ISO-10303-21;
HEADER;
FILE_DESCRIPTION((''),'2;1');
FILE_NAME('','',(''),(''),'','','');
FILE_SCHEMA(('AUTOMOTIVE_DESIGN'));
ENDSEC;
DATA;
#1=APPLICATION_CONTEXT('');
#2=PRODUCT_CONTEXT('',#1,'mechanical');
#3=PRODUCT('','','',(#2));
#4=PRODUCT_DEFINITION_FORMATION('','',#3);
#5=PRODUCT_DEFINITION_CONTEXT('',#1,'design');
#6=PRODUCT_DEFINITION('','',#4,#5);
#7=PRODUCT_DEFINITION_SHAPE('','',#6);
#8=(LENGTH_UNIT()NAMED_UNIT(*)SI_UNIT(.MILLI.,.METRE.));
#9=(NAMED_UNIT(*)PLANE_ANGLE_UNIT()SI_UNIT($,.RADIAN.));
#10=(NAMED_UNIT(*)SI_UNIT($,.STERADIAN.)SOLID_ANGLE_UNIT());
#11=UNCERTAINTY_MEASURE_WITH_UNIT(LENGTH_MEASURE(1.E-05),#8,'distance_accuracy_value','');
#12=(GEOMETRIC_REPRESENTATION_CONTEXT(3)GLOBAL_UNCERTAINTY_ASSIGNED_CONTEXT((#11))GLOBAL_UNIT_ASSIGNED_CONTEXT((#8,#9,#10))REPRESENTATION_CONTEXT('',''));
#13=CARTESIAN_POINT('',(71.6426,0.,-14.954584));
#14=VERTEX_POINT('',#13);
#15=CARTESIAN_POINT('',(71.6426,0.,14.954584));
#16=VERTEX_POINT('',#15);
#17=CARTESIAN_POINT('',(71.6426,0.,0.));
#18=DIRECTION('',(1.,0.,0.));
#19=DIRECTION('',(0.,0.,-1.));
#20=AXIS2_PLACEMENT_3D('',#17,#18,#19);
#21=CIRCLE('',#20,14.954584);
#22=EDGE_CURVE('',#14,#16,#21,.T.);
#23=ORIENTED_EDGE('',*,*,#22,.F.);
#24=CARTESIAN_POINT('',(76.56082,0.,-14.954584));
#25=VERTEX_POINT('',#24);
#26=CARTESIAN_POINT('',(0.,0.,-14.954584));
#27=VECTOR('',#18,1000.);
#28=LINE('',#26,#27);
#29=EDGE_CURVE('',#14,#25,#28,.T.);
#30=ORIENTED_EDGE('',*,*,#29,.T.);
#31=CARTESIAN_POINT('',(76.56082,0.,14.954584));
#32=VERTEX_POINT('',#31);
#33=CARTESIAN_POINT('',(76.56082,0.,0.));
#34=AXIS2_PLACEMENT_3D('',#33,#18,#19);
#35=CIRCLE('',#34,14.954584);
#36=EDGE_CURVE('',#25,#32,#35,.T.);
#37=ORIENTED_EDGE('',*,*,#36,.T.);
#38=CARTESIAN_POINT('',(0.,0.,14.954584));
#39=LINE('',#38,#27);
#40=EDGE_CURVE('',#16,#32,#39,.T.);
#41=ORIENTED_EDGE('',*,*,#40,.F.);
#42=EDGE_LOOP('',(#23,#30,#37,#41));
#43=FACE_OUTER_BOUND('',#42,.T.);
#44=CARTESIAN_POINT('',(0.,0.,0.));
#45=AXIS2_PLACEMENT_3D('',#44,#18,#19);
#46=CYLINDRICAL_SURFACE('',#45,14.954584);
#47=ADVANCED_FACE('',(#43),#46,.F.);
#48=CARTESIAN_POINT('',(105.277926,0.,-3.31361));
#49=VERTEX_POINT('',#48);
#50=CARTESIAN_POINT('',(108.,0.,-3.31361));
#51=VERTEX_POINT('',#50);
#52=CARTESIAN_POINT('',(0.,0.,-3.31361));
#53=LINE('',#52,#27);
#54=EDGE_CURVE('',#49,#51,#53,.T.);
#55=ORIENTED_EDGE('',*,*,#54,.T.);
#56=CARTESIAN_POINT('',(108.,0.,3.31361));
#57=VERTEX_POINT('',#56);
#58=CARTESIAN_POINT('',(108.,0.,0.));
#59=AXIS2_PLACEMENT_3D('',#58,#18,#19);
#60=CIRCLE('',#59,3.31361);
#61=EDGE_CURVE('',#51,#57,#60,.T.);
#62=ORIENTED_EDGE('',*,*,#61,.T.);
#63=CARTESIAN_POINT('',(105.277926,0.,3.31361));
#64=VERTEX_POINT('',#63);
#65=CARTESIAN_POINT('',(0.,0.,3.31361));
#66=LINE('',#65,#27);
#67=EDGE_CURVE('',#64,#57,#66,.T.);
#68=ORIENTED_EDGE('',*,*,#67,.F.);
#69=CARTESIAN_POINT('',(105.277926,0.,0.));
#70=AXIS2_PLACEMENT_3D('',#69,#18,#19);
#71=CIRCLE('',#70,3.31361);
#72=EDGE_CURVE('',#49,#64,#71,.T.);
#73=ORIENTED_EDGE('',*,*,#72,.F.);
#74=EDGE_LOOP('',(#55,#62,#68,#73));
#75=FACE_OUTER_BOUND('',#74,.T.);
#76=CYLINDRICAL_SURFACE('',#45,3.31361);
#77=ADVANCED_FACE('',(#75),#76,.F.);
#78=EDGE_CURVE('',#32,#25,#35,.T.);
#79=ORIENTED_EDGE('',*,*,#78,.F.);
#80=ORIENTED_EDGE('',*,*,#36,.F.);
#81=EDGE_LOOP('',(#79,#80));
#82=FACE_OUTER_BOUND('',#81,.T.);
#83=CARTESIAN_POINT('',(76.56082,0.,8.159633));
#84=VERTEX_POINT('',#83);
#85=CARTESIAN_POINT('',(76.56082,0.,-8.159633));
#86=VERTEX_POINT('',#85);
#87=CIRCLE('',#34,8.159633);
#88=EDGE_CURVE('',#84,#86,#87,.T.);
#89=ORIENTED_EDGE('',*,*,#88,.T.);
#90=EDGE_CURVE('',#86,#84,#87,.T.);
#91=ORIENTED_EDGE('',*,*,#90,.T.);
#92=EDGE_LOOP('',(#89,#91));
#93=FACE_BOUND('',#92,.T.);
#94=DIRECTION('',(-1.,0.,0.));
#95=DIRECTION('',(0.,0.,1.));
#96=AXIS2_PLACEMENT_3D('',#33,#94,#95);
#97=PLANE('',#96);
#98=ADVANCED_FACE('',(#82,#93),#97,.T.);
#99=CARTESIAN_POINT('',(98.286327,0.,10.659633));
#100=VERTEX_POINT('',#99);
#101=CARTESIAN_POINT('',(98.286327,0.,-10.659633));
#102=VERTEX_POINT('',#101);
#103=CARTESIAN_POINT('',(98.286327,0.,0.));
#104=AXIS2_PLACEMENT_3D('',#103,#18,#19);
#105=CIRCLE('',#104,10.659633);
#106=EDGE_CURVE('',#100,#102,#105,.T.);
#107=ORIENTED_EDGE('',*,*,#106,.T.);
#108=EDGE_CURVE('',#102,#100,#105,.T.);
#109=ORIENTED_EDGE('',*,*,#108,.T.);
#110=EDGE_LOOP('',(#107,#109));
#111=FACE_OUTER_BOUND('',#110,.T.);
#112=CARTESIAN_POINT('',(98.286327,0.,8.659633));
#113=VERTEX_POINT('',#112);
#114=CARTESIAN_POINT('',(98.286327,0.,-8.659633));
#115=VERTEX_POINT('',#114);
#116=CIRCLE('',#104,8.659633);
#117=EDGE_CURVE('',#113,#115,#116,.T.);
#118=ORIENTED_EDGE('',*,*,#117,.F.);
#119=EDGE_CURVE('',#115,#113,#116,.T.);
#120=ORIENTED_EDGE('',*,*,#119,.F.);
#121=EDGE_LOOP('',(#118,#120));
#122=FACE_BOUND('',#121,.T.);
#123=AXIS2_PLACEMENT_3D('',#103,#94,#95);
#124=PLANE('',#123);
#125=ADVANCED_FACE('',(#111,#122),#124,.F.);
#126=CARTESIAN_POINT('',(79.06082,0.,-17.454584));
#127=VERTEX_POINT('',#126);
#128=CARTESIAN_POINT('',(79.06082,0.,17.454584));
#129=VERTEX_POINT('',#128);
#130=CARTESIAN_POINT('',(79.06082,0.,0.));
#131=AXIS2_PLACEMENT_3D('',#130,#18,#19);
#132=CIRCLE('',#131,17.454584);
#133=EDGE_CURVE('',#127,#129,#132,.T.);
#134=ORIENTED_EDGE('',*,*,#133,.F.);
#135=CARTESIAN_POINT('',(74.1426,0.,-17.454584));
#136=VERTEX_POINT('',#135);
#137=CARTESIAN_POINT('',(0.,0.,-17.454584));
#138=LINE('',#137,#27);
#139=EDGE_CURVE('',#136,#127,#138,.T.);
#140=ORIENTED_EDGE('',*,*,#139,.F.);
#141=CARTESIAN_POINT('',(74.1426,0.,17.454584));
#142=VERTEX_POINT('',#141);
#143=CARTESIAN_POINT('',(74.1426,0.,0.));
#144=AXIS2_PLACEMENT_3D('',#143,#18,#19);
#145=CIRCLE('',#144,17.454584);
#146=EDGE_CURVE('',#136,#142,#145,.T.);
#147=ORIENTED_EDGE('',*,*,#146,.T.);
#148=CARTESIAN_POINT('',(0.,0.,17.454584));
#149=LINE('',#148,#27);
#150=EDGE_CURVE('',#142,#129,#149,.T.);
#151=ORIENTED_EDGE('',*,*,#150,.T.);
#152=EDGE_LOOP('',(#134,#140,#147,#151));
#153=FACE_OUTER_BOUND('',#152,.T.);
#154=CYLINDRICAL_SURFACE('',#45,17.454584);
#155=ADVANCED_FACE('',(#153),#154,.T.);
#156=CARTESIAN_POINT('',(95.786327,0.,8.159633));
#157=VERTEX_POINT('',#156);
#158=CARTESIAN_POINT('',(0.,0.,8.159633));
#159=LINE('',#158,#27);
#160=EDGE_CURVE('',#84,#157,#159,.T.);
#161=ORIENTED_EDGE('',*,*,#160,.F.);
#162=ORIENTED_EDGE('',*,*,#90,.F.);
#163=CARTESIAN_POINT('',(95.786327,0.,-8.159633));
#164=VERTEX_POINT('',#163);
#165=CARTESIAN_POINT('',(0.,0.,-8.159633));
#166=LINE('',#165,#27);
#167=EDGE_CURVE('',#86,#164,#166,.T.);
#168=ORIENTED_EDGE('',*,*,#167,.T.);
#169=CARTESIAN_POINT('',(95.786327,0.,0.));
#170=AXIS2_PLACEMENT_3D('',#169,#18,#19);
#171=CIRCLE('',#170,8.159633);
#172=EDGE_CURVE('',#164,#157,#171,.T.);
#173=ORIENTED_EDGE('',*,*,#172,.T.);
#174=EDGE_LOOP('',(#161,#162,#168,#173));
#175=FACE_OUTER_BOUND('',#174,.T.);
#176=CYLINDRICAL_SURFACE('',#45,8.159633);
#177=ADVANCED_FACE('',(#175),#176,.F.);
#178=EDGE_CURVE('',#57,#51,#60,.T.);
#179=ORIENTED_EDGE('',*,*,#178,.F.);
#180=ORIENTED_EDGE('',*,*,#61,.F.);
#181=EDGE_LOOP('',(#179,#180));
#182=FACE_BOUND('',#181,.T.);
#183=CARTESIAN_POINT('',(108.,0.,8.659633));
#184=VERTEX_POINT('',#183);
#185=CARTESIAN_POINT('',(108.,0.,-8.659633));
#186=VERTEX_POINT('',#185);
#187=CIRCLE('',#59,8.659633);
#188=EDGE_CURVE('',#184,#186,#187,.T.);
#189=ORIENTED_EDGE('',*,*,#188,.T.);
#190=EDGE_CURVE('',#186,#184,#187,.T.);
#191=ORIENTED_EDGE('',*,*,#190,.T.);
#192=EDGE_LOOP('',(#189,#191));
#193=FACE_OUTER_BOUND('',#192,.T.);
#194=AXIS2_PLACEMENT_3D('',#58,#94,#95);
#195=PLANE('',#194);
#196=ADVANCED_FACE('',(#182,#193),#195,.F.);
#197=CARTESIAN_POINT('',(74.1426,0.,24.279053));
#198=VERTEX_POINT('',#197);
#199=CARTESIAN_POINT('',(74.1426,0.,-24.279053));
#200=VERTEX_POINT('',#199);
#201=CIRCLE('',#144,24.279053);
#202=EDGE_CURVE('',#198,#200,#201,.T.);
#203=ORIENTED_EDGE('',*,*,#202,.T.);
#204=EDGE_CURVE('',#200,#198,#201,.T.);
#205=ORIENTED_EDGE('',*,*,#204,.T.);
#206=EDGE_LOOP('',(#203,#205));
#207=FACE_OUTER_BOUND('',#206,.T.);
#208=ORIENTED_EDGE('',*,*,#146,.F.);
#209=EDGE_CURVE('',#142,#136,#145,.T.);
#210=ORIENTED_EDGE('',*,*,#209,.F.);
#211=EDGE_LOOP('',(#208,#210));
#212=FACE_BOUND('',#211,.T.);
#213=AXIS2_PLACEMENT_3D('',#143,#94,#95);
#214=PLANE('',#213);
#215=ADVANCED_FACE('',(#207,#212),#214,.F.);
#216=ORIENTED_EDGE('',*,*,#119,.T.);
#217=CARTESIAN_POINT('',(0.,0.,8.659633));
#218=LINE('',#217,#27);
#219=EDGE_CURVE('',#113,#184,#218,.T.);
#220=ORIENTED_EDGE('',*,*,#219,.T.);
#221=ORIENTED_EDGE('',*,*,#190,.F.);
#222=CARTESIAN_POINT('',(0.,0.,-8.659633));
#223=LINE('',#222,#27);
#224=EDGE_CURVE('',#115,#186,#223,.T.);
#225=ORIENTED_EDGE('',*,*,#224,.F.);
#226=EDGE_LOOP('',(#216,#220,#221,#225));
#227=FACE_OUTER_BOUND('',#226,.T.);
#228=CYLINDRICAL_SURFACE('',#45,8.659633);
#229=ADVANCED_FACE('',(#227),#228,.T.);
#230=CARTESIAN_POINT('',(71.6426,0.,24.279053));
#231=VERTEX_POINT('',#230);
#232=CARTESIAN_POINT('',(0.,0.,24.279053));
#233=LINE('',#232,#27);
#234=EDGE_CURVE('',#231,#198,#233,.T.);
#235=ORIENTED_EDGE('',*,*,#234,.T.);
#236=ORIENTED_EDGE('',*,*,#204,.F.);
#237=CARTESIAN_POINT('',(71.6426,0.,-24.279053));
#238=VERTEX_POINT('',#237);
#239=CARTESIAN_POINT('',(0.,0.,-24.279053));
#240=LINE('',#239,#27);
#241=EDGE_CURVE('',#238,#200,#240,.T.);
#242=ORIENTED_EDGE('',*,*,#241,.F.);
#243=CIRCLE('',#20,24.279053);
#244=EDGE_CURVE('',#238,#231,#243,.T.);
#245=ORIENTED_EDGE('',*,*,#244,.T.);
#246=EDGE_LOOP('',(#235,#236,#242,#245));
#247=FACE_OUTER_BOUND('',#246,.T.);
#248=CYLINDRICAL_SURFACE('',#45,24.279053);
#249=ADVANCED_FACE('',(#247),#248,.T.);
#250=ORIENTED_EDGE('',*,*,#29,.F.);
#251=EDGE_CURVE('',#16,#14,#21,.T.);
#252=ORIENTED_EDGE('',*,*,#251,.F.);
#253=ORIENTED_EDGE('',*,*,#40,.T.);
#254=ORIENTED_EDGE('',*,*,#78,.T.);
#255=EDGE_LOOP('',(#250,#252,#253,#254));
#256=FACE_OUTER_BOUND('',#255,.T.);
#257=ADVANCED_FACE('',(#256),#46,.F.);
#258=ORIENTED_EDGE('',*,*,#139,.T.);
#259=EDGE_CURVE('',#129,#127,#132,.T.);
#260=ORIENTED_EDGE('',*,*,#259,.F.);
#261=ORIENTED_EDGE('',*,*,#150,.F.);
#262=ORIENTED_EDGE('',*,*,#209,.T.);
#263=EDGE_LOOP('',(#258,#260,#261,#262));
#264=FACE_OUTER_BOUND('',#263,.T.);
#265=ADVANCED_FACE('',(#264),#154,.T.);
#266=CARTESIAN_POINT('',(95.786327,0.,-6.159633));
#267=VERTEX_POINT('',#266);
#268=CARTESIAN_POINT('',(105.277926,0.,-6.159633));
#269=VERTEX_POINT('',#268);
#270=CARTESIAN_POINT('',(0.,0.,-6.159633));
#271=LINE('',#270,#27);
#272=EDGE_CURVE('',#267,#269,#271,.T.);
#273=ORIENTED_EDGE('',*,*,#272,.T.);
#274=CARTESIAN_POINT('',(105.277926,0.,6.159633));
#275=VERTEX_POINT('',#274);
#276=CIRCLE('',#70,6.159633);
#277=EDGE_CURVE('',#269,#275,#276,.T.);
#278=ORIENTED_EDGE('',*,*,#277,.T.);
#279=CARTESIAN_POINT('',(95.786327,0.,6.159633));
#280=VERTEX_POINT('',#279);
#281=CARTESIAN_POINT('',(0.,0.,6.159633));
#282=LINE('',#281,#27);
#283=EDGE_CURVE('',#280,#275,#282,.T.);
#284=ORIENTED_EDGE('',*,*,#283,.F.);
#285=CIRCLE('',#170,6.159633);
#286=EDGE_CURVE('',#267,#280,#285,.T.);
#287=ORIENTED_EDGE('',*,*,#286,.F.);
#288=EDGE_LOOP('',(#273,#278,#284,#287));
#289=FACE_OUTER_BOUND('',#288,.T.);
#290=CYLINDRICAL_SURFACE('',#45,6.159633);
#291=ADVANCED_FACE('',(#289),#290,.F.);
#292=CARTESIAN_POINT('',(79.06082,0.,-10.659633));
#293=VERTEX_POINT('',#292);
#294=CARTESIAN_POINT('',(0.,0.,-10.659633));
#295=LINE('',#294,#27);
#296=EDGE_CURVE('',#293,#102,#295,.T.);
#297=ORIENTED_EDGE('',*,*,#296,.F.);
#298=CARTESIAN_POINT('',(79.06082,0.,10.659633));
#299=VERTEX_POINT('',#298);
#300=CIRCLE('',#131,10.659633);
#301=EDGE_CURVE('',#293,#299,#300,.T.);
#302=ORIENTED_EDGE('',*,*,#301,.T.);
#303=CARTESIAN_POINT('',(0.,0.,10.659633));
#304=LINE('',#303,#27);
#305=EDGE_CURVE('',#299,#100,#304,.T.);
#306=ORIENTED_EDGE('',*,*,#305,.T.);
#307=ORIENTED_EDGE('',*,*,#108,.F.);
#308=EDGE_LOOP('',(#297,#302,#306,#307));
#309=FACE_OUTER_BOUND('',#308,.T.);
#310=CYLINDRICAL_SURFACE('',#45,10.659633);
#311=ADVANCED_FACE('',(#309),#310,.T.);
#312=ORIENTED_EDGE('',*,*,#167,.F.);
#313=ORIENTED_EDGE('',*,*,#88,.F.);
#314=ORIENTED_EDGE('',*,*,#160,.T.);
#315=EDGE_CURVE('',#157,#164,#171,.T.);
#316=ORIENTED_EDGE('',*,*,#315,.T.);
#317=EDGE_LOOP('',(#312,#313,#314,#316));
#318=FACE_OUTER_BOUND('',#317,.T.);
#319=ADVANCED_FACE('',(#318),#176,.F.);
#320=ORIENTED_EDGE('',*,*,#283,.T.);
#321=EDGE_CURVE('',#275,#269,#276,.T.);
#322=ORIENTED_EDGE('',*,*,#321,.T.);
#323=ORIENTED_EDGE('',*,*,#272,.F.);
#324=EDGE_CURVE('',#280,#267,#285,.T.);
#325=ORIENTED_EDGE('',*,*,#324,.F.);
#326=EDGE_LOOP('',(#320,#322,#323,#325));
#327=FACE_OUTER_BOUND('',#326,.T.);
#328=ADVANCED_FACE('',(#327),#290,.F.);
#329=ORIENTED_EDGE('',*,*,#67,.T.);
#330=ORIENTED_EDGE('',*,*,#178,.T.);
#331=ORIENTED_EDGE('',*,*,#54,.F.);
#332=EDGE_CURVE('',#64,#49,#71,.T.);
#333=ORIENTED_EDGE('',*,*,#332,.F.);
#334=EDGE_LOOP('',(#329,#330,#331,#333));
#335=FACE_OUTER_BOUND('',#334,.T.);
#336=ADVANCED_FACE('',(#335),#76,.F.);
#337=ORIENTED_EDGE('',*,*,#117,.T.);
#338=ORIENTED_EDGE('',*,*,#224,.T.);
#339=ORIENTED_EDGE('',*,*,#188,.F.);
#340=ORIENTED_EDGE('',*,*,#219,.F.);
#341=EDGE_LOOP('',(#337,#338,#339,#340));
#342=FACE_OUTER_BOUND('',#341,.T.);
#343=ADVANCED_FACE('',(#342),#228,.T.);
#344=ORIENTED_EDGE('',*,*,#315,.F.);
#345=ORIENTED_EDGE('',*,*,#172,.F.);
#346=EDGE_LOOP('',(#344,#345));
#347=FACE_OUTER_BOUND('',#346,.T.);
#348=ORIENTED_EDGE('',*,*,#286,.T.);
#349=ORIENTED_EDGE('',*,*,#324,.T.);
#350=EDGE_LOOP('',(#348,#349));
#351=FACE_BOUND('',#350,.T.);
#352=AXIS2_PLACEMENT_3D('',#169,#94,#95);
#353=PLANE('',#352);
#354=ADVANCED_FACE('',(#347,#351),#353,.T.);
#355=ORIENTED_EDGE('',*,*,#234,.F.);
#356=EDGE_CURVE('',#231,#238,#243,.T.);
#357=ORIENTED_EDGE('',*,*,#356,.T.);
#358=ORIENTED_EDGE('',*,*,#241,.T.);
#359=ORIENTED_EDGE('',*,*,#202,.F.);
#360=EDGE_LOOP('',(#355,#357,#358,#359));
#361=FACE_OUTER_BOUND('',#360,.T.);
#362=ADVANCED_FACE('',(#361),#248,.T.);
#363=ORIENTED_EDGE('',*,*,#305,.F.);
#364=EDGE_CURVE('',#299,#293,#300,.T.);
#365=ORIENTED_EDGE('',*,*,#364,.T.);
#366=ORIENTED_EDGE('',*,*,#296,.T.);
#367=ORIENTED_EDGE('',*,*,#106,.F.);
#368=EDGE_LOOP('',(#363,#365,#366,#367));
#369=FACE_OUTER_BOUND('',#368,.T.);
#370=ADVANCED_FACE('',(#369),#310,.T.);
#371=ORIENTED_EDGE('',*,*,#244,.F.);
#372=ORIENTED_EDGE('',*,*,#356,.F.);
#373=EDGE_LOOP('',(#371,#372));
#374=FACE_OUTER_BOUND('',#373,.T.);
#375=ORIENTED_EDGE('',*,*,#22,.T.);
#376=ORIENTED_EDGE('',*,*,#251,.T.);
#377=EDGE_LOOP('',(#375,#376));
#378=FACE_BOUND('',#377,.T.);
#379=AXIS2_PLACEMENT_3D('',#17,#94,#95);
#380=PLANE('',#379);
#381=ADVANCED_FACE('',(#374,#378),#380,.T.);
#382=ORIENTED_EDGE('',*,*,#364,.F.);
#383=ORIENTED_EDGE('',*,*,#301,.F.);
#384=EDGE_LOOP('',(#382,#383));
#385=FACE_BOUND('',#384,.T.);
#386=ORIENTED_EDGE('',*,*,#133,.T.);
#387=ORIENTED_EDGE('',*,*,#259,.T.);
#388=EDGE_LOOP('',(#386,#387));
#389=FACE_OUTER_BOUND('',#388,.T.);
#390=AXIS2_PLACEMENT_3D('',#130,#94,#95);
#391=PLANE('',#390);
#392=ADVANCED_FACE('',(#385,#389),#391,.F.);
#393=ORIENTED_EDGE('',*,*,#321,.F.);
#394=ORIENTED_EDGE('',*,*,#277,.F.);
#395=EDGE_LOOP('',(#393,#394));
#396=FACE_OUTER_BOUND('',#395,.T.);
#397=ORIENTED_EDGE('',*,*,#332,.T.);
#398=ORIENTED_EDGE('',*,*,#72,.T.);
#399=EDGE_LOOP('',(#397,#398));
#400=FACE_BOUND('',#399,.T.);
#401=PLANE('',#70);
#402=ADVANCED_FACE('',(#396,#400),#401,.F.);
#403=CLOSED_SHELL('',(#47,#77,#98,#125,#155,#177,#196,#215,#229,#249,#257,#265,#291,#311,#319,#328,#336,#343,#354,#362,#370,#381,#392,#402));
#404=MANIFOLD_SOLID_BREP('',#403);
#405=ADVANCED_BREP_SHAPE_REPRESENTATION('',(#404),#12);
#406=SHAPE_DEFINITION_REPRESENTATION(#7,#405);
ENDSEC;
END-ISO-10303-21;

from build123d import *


with BuildPart() as part:
    # Sketch1 → Revolve1 (revolve)
    with BuildSketch(Plane.XY, mode=Mode.PRIVATE) as revolve1_sk:
        Polygon((74.14259961, 24.279053073), (74.14259961, 17.45458405), (79.060819611, 17.45458405), (79.060819611, 10.659632807), (98.286326817, 10.659632807), (98.286326817, 8.659632807), (108, 8.659632807), (108, 3.313609887), (105.27792564, 3.313609887), (105.27792564, 6.159632807), (95.786326817, 6.159632807), (95.786326817, 8.159632807), (76.560819611, 8.159632807), (76.560819611, 14.95458405), (71.64259961, 14.95458405), (71.64259961, 24.279053073), align=None)
    revolve(revolve1_sk.sketch.rotate(Axis((0, 0, 0), (-1, 0, 0)), 90), axis=Axis((0, 0, 0), (-1, 0, 0)))


solid = part.part
